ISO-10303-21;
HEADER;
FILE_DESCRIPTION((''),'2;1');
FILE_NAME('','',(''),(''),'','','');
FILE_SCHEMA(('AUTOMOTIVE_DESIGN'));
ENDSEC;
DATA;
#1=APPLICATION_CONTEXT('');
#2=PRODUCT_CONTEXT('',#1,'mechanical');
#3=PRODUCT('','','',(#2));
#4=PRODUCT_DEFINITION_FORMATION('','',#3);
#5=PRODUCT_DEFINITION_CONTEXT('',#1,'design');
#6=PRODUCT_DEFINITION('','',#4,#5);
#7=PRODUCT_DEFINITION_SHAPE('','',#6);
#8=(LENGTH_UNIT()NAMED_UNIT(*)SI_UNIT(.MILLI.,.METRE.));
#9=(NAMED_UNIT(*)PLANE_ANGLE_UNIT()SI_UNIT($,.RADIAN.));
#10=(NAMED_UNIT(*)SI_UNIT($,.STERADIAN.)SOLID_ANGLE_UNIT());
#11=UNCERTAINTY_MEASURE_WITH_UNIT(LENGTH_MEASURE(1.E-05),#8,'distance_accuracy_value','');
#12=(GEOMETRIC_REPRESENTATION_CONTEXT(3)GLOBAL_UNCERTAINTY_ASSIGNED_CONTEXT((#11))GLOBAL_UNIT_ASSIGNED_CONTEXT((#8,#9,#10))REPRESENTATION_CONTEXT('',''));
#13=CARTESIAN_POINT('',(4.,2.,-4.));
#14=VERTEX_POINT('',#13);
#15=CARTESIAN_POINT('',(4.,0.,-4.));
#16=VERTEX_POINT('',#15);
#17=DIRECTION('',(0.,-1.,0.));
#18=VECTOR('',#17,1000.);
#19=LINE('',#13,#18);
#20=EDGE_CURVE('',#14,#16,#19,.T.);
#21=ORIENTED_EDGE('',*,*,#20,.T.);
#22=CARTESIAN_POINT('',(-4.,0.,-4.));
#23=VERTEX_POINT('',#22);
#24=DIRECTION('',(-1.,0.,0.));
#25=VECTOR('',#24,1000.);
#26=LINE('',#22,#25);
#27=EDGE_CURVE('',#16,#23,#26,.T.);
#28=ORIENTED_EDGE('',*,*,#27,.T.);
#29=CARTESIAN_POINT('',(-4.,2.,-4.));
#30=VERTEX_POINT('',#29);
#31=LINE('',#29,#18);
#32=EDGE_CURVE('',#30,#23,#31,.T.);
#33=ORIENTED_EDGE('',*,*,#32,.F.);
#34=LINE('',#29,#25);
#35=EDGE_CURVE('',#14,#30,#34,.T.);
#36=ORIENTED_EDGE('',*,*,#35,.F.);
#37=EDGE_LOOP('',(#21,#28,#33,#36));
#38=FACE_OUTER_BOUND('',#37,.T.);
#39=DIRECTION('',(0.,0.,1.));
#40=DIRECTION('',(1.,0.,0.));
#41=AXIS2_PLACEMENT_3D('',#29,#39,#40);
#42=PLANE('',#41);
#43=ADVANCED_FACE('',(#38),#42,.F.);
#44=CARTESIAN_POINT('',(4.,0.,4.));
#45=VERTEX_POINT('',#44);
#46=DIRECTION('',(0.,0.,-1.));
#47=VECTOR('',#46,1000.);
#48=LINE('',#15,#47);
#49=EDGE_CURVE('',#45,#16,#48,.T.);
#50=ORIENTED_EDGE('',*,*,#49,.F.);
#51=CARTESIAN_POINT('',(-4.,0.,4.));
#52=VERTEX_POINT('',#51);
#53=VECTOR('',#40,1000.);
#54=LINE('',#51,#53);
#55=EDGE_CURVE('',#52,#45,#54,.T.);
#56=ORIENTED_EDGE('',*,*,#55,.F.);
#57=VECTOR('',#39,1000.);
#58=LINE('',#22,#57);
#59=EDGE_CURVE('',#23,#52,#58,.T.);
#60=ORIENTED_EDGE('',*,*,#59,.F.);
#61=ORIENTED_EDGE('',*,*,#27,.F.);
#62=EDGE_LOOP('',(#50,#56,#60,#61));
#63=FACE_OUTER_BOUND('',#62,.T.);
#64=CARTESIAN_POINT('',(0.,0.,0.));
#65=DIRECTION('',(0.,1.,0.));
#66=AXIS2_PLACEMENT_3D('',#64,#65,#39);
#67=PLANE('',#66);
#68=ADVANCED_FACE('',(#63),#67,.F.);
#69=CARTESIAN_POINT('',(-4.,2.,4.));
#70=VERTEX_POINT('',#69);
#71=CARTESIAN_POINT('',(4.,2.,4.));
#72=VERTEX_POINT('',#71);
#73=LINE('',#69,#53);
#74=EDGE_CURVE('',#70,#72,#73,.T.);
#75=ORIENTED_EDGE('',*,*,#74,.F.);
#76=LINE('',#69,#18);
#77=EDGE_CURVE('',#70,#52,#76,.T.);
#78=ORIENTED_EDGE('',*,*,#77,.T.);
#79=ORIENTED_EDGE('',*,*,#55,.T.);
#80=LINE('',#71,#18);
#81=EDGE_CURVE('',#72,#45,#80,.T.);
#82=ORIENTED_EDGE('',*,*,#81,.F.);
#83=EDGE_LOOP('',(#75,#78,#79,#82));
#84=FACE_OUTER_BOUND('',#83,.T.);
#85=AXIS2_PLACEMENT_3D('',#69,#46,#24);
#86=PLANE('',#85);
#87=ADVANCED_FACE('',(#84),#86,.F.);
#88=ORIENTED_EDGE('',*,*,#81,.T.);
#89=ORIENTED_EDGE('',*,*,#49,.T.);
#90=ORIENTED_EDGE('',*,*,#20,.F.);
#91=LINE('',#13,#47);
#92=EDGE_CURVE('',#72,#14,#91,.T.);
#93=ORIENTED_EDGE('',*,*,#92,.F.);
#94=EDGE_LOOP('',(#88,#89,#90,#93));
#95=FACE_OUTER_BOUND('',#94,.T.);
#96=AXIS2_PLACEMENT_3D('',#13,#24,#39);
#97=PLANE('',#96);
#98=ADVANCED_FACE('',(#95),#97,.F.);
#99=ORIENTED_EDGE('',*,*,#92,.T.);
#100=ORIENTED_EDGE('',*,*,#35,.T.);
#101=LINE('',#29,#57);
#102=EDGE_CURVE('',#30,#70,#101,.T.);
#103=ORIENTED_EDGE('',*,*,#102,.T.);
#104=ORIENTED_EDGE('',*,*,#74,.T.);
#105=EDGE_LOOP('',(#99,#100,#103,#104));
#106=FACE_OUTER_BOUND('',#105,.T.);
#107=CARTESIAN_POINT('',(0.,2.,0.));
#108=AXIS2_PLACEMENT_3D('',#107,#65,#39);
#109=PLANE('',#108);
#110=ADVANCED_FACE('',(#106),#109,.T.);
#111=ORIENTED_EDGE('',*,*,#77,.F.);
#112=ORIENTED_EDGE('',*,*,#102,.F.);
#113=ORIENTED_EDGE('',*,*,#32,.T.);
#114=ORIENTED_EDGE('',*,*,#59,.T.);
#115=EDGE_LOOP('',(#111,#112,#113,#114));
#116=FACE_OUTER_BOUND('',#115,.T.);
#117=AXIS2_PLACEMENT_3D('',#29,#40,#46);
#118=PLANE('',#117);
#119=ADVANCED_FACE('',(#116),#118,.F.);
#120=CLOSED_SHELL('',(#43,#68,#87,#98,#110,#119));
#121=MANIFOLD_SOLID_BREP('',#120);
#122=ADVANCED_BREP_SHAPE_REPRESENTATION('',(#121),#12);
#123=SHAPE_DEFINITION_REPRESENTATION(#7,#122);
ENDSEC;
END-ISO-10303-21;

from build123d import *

# Parameters (mm, degrees)
SKETCH1_W           = 8
SKETCH1_H           = 8
BOSS_EXTRUDE1_DEPTH = 2


with BuildPart() as part:
    # Sketch1 → Boss-Extrude1 (new body)
    with BuildSketch(Plane(origin=(0, 0, 0), x_dir=(1, 0, 0), z_dir=(0, 1, 0))):
        Rectangle(SKETCH1_W, SKETCH1_H)
    extrude(amount=BOSS_EXTRUDE1_DEPTH)


solid = part.part
